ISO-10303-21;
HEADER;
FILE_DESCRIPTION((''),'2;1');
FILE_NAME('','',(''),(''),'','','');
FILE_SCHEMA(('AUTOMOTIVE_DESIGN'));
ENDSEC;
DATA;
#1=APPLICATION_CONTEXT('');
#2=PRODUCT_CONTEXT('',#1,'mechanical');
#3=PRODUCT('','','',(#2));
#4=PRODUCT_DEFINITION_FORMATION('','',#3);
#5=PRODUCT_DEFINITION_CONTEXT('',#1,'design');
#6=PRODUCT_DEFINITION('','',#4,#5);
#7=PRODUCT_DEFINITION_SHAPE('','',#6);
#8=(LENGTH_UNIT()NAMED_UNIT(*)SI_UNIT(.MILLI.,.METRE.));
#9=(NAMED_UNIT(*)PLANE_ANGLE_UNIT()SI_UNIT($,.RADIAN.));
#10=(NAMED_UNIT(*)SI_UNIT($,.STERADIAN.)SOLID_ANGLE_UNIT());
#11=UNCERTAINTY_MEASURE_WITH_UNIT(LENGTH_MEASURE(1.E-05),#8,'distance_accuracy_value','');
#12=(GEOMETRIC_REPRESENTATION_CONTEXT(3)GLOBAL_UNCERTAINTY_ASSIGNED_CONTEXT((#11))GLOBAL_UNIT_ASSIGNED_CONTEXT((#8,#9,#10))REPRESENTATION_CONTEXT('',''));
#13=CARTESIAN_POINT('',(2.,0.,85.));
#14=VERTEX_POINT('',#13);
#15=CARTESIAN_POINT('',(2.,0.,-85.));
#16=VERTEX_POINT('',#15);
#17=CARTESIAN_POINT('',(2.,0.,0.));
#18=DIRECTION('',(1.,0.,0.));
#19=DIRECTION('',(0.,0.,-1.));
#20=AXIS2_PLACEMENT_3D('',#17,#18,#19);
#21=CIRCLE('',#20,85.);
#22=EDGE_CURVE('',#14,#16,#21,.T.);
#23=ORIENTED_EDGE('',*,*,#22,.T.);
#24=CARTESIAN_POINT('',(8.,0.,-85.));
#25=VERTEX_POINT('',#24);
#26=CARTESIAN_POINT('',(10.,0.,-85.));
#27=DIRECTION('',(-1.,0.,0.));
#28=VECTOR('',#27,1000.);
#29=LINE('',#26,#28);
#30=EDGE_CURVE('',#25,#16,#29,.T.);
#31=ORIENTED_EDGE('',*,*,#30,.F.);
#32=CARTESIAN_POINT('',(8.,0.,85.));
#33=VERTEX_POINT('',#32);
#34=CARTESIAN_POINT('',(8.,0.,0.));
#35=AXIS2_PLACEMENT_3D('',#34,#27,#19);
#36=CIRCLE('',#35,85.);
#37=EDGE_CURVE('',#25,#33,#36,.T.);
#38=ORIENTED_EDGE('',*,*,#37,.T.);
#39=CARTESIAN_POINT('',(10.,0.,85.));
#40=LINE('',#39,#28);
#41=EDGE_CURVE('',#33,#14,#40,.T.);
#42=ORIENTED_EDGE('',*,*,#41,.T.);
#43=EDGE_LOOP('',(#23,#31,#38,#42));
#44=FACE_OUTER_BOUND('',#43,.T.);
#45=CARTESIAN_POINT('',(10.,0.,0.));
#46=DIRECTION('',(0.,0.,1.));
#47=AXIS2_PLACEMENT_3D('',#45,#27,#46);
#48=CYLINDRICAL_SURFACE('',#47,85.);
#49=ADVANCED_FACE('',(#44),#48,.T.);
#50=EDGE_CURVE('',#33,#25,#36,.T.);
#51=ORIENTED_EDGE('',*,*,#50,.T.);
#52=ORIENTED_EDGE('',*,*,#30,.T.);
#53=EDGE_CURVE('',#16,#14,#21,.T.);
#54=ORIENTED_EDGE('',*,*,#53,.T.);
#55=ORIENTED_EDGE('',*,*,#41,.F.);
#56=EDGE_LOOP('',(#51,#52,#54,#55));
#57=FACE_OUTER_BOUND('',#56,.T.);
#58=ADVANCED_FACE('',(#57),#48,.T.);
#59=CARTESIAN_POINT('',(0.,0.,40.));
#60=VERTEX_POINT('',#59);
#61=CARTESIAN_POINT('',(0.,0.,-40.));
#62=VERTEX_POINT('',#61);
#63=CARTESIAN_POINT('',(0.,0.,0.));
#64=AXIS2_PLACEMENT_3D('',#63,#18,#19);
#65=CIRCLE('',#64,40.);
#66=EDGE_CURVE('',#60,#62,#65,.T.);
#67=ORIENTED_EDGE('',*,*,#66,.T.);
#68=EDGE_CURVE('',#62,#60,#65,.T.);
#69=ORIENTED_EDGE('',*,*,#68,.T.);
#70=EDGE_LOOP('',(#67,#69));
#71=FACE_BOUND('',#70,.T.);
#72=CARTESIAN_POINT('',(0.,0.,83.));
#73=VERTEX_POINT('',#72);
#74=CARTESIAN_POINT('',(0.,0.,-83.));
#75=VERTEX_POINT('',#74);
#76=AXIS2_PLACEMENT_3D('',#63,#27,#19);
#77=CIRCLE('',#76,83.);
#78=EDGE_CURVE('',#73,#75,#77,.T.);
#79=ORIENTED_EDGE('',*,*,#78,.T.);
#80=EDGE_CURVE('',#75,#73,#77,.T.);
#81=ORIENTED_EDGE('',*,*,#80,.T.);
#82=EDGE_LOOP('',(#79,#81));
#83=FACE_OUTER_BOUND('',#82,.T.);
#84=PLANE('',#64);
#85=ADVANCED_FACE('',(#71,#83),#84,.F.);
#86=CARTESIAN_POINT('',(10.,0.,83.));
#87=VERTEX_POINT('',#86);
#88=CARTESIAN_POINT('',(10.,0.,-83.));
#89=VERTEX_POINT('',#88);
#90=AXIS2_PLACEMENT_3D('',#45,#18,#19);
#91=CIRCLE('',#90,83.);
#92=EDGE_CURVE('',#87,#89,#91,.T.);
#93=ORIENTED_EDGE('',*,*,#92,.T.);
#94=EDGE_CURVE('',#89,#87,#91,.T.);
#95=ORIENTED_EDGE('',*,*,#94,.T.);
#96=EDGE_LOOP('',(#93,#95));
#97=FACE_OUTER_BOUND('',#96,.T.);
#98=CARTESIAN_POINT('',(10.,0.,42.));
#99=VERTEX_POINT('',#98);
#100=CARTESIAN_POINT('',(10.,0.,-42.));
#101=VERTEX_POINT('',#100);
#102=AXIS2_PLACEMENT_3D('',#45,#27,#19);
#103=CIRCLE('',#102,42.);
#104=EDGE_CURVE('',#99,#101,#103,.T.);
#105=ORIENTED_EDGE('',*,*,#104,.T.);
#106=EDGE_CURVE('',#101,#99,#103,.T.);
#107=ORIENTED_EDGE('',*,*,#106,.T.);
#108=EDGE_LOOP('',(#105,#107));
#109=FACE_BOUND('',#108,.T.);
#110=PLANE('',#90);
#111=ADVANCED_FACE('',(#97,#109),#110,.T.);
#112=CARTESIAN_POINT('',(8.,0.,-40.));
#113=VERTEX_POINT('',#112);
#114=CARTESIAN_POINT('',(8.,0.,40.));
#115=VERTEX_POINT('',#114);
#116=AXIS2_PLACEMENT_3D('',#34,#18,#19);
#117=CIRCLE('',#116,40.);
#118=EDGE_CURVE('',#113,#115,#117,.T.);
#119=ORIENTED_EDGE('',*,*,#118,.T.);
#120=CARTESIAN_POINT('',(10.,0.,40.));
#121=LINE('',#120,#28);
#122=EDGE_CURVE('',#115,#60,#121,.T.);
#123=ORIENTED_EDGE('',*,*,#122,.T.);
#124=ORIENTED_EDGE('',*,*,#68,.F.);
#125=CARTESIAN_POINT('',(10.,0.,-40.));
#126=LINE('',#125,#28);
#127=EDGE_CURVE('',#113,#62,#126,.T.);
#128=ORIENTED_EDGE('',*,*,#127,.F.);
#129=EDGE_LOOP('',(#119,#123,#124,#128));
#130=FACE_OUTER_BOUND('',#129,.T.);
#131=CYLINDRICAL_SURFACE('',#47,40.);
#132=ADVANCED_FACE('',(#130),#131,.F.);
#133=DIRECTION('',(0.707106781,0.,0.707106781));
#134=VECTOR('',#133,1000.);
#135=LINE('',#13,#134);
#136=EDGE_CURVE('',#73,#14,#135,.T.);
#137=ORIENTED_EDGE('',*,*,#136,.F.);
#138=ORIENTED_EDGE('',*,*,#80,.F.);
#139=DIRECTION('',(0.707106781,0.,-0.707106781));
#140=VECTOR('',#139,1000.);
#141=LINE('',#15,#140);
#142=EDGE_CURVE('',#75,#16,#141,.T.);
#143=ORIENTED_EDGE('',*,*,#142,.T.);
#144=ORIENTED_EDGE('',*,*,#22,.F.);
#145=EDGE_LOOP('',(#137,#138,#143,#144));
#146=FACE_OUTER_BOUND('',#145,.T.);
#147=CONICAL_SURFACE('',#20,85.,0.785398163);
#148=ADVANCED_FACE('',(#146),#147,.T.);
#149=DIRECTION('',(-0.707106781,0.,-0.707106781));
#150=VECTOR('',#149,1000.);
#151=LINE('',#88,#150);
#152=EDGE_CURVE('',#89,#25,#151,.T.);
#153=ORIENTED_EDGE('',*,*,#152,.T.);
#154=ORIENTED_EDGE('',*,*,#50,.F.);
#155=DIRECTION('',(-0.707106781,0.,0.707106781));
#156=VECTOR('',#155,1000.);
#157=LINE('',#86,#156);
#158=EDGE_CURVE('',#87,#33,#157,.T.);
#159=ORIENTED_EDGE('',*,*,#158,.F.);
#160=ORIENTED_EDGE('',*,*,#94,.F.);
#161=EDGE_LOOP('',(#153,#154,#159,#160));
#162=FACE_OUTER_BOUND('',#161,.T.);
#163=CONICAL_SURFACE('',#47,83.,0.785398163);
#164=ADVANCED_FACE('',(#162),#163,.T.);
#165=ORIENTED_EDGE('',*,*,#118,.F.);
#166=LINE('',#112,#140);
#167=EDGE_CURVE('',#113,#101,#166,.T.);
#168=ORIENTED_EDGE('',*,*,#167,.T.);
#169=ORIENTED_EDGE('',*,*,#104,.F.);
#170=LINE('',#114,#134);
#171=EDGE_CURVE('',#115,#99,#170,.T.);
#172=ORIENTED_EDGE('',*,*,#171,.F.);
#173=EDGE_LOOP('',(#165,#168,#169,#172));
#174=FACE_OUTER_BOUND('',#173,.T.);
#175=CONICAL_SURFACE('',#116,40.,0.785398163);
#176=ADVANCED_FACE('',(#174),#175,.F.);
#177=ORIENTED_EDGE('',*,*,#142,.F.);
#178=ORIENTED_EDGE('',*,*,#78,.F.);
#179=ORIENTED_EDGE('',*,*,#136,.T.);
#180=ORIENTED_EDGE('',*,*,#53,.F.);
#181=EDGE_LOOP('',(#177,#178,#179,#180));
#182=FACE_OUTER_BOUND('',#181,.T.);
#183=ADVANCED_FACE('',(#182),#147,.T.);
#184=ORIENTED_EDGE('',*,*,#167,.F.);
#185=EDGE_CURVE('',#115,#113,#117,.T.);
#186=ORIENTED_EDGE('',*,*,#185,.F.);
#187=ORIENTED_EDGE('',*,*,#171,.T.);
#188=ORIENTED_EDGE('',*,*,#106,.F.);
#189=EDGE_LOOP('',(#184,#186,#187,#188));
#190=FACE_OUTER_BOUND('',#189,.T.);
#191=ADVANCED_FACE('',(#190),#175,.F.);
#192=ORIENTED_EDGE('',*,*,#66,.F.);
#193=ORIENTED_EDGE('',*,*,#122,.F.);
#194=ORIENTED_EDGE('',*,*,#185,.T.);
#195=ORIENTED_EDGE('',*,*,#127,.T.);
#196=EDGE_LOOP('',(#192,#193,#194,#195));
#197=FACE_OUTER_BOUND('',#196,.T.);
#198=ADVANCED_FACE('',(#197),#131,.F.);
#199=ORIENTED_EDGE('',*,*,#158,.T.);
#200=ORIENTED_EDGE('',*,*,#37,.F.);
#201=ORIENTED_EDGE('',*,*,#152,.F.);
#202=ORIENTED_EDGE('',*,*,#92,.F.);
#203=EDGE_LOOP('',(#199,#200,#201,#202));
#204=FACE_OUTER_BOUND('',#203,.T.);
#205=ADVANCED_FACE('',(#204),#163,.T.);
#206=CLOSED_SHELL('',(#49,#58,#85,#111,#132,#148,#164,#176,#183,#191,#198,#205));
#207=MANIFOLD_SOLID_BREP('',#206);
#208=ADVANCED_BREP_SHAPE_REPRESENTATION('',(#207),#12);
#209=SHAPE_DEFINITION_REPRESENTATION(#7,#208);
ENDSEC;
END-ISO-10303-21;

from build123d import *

# Parameters (mm, degrees)
SKETCH1_R           = 85
SKETCH1_R_2         = 40
BOSS_EXTRUDE1_DEPTH = 10
CHAMFER1_SIZE       = 2


with BuildPart() as part:
    # Sketch1 → Boss-Extrude1 (new body)
    with BuildSketch(Plane(origin=(0, 0, 0), x_dir=(0, 0, -1), z_dir=(1, 0, 0))):
        Circle(SKETCH1_R)
        Circle(SKETCH1_R_2, mode=Mode.SUBTRACT)
    extrude(amount=BOSS_EXTRUDE1_DEPTH)

    # Chamfer1
    chamfer1_edges = [part.edges().sort_by_distance(p)[0] for p in [
        (0, 0, 85),
        (10, 0, 85),
        (10, 0, 40),
    ]]
    chamfer(chamfer1_edges, length=CHAMFER1_SIZE)


solid = part.part
